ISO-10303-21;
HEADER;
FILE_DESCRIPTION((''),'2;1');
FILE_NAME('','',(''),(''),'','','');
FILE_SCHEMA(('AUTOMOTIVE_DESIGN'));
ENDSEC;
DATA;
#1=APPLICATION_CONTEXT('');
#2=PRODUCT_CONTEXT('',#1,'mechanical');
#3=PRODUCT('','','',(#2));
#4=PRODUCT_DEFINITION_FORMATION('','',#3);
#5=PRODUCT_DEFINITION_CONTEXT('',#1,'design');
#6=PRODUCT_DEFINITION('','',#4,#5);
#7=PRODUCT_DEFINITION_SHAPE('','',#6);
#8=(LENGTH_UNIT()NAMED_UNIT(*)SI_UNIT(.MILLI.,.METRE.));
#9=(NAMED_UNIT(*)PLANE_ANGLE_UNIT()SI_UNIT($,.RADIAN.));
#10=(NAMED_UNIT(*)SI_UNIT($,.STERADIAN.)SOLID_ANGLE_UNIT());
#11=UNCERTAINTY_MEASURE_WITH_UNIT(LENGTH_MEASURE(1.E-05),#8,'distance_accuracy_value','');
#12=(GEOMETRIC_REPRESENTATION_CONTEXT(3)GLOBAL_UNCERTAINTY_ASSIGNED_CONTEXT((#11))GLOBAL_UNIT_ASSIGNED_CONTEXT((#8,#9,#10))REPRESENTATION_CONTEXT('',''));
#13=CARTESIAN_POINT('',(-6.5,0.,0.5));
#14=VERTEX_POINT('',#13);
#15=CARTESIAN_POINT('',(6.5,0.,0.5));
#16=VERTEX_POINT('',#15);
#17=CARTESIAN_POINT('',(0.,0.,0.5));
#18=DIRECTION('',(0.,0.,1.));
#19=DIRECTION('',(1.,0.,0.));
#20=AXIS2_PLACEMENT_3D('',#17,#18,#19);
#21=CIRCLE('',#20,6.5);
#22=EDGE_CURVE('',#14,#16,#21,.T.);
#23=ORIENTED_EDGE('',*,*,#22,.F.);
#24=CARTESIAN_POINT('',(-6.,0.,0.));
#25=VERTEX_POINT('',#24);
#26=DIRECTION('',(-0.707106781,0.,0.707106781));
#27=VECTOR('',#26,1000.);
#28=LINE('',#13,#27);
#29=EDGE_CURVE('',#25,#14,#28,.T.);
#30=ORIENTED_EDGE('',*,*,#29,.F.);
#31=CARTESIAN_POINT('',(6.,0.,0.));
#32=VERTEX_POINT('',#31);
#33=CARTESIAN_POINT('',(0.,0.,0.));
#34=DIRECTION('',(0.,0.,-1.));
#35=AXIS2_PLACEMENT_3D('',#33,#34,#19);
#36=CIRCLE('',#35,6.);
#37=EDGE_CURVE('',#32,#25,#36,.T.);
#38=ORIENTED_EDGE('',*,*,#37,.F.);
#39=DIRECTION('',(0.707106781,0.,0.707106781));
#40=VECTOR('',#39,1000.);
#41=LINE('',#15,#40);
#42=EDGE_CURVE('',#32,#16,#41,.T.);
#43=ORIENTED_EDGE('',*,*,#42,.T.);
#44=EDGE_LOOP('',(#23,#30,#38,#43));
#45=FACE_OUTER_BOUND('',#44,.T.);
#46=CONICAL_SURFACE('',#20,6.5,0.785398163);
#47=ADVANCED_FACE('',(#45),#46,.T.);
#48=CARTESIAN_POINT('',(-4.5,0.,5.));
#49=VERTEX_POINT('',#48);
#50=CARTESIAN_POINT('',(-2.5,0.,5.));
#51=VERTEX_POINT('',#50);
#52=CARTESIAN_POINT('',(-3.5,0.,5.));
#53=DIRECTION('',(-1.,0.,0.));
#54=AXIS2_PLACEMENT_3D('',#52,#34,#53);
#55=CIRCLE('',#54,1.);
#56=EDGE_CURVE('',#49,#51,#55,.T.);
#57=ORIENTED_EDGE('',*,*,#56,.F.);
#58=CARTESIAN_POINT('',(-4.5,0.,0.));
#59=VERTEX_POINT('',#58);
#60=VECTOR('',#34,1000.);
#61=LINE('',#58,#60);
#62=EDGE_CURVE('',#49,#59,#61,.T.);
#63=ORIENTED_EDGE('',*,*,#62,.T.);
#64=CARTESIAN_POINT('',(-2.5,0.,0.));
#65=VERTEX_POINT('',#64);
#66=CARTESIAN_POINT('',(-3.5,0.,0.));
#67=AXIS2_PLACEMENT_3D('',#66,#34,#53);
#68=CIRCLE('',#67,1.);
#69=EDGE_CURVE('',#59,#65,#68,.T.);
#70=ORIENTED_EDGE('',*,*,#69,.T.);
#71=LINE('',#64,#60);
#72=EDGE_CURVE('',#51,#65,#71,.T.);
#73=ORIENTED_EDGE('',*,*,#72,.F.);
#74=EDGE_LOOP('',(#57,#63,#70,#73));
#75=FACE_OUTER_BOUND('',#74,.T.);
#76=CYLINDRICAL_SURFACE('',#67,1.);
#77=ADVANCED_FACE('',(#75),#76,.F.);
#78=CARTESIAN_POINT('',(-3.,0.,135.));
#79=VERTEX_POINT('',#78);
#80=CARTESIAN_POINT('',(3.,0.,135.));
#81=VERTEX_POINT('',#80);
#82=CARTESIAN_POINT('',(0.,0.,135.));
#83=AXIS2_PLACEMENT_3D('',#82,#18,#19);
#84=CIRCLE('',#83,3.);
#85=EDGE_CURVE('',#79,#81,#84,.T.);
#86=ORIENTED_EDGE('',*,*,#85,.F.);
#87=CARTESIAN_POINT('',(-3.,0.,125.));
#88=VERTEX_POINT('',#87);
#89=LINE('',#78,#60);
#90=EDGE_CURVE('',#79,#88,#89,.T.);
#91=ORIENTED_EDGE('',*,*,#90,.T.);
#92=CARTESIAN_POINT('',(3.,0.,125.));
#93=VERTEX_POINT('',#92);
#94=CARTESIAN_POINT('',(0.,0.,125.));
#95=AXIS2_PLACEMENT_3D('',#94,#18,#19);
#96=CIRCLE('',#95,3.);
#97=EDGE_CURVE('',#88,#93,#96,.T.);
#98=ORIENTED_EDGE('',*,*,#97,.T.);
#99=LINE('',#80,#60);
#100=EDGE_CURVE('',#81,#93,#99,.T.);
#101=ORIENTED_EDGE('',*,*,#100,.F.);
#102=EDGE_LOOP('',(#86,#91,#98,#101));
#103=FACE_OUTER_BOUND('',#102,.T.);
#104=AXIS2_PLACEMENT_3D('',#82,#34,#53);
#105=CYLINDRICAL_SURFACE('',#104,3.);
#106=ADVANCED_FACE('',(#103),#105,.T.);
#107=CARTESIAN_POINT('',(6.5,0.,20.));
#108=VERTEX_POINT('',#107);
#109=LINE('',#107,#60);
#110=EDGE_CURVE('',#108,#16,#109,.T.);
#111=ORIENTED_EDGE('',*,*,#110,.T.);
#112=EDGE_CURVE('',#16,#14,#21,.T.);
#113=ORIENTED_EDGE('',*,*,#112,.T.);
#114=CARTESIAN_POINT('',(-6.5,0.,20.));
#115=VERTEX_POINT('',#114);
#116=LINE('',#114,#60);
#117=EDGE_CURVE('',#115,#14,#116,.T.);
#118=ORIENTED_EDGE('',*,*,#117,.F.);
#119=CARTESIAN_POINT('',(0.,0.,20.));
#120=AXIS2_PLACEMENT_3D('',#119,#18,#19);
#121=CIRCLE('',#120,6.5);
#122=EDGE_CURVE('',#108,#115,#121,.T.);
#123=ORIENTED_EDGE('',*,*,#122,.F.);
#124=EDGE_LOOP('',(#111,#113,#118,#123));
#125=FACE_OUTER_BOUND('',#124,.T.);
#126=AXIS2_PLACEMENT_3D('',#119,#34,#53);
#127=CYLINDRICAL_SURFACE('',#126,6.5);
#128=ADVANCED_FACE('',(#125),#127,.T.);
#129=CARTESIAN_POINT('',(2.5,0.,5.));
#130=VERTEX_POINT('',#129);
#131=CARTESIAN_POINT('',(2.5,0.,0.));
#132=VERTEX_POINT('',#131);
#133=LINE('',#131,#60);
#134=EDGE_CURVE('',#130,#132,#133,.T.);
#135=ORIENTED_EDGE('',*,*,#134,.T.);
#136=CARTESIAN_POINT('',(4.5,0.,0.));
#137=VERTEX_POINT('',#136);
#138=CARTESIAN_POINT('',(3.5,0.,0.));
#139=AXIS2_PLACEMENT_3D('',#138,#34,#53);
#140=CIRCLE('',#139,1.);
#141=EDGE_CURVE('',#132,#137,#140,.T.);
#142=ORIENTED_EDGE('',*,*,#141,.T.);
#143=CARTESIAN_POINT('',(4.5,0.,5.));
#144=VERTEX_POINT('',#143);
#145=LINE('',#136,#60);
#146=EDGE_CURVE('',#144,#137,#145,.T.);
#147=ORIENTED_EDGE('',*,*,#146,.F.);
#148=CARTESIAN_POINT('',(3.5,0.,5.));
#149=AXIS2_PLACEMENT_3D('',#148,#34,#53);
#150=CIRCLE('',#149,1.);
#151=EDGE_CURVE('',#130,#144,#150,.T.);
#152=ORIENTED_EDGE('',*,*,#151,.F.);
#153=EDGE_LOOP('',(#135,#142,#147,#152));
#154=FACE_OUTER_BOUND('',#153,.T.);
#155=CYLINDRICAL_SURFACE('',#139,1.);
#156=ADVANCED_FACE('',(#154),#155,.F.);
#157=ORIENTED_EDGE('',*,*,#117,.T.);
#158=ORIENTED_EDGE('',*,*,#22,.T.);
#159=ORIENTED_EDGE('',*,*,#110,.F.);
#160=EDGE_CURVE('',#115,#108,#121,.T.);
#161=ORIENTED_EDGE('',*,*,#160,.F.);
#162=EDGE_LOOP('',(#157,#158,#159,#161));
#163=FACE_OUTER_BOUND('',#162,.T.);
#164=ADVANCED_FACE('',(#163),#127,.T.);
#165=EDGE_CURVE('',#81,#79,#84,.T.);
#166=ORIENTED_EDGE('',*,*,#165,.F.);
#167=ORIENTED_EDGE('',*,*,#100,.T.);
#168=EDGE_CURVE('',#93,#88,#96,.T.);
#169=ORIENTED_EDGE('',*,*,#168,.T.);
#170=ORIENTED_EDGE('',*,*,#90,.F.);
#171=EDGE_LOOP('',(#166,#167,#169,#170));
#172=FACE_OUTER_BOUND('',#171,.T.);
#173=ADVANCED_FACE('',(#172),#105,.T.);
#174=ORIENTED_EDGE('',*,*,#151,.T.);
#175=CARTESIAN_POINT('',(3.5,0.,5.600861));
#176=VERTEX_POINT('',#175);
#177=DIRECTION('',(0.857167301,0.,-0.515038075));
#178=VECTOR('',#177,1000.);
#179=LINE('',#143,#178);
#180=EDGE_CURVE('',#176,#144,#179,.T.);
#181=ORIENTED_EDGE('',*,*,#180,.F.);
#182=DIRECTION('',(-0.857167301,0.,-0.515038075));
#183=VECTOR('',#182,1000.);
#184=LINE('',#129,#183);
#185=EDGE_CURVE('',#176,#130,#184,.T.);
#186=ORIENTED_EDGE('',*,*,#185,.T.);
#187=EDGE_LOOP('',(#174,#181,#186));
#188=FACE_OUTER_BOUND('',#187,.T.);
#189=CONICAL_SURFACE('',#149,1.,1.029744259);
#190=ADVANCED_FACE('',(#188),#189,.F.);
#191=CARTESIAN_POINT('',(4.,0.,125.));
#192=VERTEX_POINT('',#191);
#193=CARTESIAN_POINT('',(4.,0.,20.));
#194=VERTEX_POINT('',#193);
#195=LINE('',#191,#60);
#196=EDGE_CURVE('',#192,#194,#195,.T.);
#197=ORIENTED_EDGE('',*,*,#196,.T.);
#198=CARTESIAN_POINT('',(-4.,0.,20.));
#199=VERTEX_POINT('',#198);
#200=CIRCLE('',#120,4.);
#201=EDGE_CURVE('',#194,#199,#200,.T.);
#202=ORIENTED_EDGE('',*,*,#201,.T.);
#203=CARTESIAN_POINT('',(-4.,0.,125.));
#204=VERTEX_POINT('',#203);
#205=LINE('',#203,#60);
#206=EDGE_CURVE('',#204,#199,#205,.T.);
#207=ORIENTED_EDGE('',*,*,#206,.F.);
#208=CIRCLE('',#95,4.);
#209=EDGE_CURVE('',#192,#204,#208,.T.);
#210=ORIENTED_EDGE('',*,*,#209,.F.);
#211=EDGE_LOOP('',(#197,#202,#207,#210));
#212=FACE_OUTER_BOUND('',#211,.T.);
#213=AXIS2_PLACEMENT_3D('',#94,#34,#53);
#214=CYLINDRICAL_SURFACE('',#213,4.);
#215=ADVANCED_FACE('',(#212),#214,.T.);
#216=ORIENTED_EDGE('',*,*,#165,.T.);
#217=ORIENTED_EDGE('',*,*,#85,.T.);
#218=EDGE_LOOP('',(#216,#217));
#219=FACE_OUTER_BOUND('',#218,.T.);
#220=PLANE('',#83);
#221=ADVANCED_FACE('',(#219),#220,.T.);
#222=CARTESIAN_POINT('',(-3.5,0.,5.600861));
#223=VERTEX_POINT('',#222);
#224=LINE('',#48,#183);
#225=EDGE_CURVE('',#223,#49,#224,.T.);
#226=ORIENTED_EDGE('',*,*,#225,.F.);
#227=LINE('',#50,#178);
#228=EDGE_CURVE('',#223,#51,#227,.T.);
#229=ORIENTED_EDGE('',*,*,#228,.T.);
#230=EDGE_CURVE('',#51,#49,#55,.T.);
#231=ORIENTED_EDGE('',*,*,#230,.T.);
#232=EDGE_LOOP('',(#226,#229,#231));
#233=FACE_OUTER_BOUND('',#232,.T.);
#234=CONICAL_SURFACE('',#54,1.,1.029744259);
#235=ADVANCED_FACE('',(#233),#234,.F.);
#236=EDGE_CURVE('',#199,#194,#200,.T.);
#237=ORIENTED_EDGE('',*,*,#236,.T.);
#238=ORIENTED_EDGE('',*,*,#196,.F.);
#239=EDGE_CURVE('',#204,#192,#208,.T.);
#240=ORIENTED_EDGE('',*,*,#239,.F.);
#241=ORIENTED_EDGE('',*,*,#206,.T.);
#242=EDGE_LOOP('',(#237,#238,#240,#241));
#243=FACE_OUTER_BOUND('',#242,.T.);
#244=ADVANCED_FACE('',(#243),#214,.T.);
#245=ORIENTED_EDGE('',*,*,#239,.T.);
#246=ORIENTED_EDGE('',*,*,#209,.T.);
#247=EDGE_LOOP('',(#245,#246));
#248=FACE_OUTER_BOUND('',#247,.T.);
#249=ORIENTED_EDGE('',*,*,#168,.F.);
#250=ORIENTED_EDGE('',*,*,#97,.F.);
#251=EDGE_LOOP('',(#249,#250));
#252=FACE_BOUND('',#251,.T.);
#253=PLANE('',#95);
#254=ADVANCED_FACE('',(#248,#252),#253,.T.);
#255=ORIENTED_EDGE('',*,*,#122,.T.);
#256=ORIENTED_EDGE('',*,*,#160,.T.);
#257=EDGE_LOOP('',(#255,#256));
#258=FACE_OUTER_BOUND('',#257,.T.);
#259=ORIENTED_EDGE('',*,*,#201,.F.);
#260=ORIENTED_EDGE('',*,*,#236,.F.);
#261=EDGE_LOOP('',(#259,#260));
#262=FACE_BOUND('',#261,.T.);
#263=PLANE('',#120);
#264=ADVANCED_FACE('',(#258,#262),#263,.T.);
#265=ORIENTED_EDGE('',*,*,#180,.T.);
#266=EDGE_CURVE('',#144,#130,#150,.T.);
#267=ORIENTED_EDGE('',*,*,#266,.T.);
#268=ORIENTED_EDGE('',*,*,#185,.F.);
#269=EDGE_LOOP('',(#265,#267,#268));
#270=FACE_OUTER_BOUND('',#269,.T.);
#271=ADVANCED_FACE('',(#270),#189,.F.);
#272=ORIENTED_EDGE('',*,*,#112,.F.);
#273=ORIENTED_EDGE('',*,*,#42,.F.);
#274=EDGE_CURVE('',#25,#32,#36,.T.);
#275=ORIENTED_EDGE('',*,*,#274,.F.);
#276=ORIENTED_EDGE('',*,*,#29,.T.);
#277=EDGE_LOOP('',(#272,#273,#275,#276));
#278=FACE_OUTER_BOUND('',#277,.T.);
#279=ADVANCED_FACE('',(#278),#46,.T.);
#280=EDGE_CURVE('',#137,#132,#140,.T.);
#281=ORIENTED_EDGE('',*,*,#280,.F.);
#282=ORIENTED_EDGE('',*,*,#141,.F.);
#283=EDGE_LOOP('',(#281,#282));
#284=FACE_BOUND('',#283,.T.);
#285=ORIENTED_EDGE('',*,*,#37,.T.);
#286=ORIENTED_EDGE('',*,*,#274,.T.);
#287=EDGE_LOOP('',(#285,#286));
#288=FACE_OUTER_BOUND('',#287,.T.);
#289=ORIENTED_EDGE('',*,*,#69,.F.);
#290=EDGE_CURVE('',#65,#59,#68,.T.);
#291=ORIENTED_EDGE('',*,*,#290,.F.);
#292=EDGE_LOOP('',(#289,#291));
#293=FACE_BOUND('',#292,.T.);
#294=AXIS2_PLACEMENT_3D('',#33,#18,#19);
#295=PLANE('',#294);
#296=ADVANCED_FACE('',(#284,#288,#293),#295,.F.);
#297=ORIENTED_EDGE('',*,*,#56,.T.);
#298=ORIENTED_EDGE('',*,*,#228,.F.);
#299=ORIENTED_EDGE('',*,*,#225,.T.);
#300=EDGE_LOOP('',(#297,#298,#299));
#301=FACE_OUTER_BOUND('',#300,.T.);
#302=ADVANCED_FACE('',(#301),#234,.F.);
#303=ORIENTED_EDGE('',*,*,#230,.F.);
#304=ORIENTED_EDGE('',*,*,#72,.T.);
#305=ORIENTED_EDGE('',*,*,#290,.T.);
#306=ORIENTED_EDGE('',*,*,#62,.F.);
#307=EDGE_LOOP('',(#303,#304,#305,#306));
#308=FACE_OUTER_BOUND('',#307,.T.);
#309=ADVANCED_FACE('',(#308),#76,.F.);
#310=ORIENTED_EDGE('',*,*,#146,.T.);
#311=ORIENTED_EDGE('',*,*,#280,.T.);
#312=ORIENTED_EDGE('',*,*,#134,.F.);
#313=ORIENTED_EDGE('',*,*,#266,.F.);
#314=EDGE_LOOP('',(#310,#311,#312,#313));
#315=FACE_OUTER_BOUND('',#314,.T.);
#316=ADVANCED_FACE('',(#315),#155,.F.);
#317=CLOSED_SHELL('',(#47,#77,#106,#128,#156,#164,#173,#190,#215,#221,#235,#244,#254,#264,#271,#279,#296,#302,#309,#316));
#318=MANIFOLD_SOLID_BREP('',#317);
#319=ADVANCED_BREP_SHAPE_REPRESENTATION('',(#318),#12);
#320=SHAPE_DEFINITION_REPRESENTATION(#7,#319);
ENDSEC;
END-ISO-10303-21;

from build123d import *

# Parameters (mm, degrees)
SKETCH_1_R                = 6.5
EXTRUDE_1_DEPTH           = 20
CHAMFER_1_SIZE            = 0.5
HOLE_WIZARD_2_0_2_1_D     = 2
HOLE_WIZARD_2_0_2_1_DEPTH = 5
HOLE_WIZARD_2_0_2_1_TIP   = 0.600860619
SKETCH_8_R                = 4
EXTRUDE_2_DEPTH           = 105
SKETCH_9_R                = 3
EXTRUDE_3_DEPTH           = 10


with BuildPart() as part:
    # 草图1 → 凸台-拉伸1 (new body)
    with BuildSketch(Plane.XY):
        Circle(SKETCH_1_R)
    extrude(amount=EXTRUDE_1_DEPTH)

    # 倒角1
    chamfer_1_edges = [part.edges().sort_by_distance(p)[0] for p in [
        (-6.5, 0, 0),
    ]]
    chamfer(chamfer_1_edges, length=CHAMFER_1_SIZE)

    # Ø2.0 (2) 直径孔1
    with Locations(Plane(origin=(0, 0, 0), x_dir=(-1, 0, 0), z_dir=(0, 0, -1))):
        with Locations((-3.5, 0), (3.5, 0)):
            Hole(HOLE_WIZARD_2_0_2_1_D / 2, depth=HOLE_WIZARD_2_0_2_1_DEPTH)
            with Locations((0, 0, -(HOLE_WIZARD_2_0_2_1_DEPTH + HOLE_WIZARD_2_0_2_1_TIP / 2))):  # 118° drill point
                Cone(0, HOLE_WIZARD_2_0_2_1_D / 2, HOLE_WIZARD_2_0_2_1_TIP, mode=Mode.SUBTRACT)

    # 草图8 → 凸台-拉伸2 (add)
    with BuildSketch(Plane.XY.offset(20)):
        Circle(SKETCH_8_R)
    extrude(amount=EXTRUDE_2_DEPTH)

    # 草图9 → 凸台-拉伸3 (add)
    with BuildSketch(Plane.XY.offset(125)):
        Circle(SKETCH_9_R)
    extrude(amount=EXTRUDE_3_DEPTH)


solid = part.part
